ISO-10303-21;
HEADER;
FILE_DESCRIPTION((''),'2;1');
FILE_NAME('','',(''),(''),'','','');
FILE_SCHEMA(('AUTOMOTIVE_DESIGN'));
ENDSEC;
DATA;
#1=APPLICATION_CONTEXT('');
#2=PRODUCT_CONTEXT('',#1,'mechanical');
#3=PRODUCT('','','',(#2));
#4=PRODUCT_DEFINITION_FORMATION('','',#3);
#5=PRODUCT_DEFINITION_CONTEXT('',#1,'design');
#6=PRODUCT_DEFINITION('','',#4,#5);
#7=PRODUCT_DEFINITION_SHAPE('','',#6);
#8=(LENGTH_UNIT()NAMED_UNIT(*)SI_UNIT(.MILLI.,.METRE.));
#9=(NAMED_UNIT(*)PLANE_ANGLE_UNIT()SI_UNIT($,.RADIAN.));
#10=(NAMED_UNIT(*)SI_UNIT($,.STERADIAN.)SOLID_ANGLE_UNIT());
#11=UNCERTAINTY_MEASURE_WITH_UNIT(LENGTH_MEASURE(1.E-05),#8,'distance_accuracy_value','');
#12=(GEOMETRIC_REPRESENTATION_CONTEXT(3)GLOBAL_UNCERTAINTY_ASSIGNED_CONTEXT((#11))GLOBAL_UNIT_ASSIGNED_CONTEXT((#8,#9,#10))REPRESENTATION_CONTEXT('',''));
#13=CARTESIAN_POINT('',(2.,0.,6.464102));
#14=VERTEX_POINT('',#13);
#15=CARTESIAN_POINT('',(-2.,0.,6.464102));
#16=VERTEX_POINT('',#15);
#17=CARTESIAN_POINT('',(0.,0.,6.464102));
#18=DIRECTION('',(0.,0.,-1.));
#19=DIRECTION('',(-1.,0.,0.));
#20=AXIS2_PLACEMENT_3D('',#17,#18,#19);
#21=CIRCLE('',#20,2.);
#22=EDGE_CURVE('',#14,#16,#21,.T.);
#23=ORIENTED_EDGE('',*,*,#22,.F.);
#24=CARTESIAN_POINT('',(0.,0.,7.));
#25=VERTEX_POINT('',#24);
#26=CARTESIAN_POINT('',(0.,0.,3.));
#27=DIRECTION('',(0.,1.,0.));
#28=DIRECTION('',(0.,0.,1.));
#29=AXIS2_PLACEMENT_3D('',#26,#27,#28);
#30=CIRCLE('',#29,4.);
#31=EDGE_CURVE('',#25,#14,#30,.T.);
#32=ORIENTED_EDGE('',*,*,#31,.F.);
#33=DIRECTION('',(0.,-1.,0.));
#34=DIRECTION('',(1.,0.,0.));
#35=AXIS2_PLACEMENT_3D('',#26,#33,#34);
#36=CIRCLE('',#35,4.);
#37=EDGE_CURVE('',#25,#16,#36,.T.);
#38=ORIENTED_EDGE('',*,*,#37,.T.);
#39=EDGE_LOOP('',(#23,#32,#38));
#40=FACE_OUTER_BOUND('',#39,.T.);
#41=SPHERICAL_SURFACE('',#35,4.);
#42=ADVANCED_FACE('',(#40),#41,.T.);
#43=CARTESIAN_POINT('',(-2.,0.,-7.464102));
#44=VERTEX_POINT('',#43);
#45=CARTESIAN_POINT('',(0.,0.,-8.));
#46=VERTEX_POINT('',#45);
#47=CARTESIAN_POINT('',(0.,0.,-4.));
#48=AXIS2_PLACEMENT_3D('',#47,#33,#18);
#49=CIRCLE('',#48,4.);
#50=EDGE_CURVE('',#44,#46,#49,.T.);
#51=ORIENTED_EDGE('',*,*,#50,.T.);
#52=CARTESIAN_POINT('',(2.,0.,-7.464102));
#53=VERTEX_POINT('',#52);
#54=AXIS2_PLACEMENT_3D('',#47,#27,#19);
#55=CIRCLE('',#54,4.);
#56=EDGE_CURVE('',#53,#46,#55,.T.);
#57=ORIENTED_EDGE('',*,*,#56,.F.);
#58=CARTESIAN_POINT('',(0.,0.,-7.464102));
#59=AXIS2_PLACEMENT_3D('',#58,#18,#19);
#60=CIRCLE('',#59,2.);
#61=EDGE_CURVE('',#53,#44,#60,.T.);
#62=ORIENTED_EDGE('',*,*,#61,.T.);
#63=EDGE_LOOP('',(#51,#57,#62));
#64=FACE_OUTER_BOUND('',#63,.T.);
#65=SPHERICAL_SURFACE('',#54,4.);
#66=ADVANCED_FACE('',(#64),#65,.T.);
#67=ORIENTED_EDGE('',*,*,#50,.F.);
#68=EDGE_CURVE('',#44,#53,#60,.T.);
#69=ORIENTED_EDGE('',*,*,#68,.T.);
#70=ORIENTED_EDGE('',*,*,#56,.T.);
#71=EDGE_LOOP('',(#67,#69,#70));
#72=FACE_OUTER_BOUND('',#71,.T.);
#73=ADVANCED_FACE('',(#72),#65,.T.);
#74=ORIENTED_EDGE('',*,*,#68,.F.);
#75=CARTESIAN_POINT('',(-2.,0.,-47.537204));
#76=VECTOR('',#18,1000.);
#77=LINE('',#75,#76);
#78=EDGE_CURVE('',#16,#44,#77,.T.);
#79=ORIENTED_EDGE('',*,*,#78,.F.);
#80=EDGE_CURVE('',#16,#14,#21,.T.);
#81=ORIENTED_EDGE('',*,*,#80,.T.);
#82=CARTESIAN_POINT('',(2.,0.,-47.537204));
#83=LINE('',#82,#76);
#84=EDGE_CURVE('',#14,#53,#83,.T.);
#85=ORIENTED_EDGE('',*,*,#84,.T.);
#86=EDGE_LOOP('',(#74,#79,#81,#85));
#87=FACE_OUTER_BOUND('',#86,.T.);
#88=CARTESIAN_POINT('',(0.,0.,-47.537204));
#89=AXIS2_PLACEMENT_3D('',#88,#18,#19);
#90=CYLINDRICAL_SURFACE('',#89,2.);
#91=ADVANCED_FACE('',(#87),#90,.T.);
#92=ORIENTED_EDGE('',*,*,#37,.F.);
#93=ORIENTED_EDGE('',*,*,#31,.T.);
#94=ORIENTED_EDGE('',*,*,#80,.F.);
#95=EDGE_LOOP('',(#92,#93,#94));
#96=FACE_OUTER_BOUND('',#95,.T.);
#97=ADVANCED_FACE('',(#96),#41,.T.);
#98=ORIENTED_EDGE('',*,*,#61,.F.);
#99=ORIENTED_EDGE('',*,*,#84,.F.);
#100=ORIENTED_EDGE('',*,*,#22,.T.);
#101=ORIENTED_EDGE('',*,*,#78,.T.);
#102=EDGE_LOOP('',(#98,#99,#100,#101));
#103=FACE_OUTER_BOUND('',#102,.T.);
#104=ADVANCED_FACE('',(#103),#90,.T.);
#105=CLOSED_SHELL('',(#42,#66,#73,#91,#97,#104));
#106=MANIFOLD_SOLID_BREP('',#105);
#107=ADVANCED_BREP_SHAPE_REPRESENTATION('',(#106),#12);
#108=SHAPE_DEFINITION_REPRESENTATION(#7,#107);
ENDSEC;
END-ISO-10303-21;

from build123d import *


with BuildPart() as part:
    # Logo3_bib1 → Revolve1 (revolve)
    with BuildSketch(Plane(origin=(0, 0, 0), x_dir=(-1, 0, 0), z_dir=(0, -1, 0))):
        with BuildLine():
            Line((0, 8), (0, -7))
            ThreePointArc((0, -7), (1.03527618, -6.863703305), (2, -6.464101615))
            Line((2, -6.464101615), (2, 7.464101615))
            ThreePointArc((2, 7.464101615), (1.03527618, 7.863703305), (0, 8))
        make_face()
    revolve(axis=Axis((0, 0, -47.537203702), (0, 0, 1)))


solid = part.part
